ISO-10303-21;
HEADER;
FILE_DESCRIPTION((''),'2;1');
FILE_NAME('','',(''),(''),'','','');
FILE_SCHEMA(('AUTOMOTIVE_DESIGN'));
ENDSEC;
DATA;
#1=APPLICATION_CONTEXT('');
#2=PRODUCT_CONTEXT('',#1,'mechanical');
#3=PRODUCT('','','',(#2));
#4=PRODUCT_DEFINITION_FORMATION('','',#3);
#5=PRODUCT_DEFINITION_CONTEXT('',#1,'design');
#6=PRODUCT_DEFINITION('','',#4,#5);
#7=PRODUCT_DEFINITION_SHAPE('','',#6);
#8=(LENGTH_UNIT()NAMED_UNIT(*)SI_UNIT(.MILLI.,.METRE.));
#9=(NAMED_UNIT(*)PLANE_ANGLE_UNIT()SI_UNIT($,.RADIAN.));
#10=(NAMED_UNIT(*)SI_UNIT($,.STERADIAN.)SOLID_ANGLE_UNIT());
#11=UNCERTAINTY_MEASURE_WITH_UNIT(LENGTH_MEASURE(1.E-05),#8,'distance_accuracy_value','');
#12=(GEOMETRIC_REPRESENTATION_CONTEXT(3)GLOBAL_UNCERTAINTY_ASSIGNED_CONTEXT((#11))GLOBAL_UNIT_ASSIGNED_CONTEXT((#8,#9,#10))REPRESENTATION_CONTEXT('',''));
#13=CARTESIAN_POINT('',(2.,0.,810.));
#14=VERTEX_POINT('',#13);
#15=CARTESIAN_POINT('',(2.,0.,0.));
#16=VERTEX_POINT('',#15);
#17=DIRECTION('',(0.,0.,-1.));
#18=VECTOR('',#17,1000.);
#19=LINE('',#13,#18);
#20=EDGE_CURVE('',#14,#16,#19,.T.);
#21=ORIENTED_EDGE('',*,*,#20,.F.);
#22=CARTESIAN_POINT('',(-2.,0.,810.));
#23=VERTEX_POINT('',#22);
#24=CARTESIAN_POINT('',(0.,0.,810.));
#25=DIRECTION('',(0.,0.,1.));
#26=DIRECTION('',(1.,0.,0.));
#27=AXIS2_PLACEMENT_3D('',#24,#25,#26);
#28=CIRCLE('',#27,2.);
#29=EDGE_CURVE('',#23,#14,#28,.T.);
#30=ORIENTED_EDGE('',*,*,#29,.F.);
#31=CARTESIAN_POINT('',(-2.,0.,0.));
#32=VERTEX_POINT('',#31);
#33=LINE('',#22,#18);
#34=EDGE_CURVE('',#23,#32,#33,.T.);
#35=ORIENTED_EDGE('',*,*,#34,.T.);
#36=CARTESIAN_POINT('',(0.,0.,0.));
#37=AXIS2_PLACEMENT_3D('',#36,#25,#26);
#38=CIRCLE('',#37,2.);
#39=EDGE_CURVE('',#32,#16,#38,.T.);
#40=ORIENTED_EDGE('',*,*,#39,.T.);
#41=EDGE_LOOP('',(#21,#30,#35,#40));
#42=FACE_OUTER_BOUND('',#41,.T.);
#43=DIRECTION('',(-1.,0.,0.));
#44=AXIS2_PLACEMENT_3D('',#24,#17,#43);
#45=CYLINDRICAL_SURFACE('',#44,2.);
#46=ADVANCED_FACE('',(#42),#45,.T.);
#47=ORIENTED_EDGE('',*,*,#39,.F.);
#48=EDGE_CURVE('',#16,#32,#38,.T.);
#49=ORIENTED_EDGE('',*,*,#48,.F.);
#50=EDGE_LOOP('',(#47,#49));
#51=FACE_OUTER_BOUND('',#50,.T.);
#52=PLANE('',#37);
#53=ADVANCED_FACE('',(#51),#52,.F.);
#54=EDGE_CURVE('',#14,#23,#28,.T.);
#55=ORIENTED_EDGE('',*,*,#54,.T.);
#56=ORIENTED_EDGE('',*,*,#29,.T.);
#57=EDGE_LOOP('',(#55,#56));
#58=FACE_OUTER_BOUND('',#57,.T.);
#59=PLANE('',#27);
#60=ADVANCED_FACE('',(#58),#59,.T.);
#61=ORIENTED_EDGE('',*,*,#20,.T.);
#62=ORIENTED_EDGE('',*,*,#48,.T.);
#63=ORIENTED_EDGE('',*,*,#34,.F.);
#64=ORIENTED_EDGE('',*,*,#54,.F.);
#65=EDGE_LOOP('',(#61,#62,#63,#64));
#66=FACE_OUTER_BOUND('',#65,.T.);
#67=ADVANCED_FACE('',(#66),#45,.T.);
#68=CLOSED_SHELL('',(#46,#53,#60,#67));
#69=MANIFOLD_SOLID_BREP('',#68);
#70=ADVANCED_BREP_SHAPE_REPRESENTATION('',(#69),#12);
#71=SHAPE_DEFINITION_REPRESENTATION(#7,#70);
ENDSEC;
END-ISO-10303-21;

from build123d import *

# Parameters (mm, degrees)
SKETCH2_R           = 2
BOSS_EXTRUDE1_DEPTH = 810


with BuildPart() as part:
    # Sketch2 → Boss-Extrude1 (new body)
    with BuildSketch(Plane.XY):
        Circle(SKETCH2_R)
    extrude(amount=BOSS_EXTRUDE1_DEPTH)


solid = part.part
